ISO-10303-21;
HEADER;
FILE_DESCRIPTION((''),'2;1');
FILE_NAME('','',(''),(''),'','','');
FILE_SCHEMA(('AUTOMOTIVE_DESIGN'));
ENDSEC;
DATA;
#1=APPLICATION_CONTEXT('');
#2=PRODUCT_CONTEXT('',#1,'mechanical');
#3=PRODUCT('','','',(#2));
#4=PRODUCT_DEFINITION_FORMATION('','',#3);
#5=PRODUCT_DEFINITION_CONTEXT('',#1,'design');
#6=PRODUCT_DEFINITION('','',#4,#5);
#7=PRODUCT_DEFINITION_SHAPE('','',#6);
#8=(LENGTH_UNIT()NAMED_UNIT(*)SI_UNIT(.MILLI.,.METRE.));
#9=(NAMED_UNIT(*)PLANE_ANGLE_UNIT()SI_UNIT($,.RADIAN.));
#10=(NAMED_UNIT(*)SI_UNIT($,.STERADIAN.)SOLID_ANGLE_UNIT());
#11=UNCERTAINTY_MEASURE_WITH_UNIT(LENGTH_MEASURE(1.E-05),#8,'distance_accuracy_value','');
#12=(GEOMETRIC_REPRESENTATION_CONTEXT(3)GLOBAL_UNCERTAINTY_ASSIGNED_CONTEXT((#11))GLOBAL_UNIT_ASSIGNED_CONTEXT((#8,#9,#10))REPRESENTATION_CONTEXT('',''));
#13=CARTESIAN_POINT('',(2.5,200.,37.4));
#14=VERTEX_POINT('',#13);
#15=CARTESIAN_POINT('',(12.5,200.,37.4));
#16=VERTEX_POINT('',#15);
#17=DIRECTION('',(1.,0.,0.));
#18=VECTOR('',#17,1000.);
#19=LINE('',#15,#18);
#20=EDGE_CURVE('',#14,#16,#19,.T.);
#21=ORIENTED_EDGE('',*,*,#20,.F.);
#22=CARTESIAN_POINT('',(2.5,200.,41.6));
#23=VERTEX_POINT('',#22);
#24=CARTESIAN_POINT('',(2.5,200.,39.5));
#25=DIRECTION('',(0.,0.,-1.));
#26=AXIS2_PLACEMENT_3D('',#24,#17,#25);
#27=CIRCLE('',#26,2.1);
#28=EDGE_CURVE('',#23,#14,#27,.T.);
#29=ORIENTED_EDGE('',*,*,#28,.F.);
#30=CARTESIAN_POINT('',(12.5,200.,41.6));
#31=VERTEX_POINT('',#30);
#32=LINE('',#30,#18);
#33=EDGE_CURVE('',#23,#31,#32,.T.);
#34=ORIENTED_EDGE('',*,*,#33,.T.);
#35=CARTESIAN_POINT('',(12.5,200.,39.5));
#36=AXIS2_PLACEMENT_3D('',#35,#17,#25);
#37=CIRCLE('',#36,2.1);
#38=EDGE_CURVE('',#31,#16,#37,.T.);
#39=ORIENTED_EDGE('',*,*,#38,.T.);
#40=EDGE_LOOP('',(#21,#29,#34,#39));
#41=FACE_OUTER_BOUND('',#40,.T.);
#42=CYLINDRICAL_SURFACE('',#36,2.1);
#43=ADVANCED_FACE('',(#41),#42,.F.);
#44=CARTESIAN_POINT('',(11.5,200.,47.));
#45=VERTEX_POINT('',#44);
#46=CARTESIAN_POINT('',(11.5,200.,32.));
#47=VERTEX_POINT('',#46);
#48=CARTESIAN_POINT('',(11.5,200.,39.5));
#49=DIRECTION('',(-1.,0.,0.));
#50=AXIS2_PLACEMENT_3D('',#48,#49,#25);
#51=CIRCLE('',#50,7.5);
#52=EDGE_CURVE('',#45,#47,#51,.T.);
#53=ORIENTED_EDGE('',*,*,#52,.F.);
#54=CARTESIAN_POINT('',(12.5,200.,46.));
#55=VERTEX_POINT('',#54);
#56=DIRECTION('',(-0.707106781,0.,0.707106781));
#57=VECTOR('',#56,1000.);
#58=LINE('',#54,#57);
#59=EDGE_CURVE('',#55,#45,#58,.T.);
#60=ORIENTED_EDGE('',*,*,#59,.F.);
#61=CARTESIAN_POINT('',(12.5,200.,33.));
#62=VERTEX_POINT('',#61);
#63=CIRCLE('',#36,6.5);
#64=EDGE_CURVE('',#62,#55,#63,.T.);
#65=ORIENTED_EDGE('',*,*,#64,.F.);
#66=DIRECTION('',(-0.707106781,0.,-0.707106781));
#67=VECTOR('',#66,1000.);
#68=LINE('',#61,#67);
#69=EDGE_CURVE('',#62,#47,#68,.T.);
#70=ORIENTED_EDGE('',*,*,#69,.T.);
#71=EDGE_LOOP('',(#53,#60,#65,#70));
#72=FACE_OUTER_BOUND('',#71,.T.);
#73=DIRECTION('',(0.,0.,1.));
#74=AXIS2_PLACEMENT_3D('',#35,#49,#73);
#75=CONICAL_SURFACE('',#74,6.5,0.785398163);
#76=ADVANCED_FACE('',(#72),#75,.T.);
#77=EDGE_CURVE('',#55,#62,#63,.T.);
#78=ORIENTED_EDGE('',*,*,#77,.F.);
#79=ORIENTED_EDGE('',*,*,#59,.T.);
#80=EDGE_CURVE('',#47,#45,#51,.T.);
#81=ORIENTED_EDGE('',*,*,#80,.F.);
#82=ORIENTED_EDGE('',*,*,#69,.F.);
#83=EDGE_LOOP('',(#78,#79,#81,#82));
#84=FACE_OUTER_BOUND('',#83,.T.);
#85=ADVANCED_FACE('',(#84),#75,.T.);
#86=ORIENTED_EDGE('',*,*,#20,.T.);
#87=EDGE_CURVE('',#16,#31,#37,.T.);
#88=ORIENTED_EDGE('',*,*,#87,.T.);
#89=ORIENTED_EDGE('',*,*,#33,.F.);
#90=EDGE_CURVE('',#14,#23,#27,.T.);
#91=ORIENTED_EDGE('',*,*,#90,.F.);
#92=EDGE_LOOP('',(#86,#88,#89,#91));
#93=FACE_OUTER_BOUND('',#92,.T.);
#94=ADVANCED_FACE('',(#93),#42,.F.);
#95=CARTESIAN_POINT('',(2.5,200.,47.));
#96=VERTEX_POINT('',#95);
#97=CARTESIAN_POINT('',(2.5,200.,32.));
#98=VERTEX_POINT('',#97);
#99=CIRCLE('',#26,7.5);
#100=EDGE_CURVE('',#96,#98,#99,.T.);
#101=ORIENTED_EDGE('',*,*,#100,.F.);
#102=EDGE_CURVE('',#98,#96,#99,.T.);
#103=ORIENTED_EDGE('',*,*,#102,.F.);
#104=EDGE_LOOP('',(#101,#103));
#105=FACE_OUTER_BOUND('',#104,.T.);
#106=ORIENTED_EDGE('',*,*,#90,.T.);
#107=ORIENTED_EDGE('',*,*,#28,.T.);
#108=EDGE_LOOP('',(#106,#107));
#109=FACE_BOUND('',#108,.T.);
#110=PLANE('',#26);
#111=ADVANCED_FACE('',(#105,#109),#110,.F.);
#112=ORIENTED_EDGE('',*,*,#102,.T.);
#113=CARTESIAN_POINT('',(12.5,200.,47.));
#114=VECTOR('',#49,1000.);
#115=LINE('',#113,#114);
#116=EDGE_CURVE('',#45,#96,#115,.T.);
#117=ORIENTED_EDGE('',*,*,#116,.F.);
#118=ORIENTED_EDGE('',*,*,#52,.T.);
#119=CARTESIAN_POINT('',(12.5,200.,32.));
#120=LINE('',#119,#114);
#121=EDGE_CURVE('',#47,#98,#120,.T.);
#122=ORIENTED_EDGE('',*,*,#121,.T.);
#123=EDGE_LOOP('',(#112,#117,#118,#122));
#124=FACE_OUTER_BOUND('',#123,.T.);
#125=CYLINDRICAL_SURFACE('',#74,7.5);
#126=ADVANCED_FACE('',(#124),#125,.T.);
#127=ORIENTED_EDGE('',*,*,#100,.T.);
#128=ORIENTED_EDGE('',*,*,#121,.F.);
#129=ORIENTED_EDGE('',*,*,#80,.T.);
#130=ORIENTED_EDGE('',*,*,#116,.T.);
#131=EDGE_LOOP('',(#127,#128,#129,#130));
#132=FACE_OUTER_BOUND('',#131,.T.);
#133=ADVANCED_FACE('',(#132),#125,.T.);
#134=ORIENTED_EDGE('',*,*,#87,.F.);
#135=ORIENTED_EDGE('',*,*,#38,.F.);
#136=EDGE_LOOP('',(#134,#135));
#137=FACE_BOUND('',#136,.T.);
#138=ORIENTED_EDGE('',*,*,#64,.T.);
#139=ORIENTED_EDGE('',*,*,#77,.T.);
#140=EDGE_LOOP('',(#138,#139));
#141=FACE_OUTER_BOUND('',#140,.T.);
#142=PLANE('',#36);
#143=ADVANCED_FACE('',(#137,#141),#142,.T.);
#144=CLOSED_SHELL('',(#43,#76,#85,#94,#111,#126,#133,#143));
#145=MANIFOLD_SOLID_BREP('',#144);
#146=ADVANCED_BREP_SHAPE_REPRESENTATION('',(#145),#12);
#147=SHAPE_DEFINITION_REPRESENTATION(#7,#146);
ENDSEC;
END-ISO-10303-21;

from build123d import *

# Parameters (mm, degrees)
SKETCH1_R             = 7.5
BOSS_EXTRUDE1_DEPTH   = 10
CHAMFER1_SIZE         = 1
M5_TAPPED_HOLE1_D     = 4.2
M5_TAPPED_HOLE1_DEPTH = 10
M5_TAPPED_HOLE1_TIP   = 1.2618073


with BuildPart() as part:
    # Sketch1 → Boss-Extrude1 (new body)
    with BuildSketch(Plane(origin=(2.5, 0, 0), x_dir=(0, 0, -1), z_dir=(1, 0, 0))):
        with Locations((-39.5, 200)):
            Circle(SKETCH1_R)
    extrude(amount=BOSS_EXTRUDE1_DEPTH)

    # Chamfer1
    chamfer1_edges = [part.edges().sort_by_distance(p)[0] for p in [
        (12.5, 200, 47),
    ]]
    chamfer(chamfer1_edges, length=CHAMFER1_SIZE)

    # M5 Tapped Hole1
    with Locations(Plane(origin=(12.5, 200, 39.5), x_dir=(0, 0, 1), z_dir=(1, 0, 0))):
        with Locations((0, 0)):
            Hole(M5_TAPPED_HOLE1_D / 2, depth=M5_TAPPED_HOLE1_DEPTH)
            with Locations((0, 0, -(M5_TAPPED_HOLE1_DEPTH + M5_TAPPED_HOLE1_TIP / 2))):  # 118° drill point
                Cone(0, M5_TAPPED_HOLE1_D / 2, M5_TAPPED_HOLE1_TIP, mode=Mode.SUBTRACT)


solid = part.part
